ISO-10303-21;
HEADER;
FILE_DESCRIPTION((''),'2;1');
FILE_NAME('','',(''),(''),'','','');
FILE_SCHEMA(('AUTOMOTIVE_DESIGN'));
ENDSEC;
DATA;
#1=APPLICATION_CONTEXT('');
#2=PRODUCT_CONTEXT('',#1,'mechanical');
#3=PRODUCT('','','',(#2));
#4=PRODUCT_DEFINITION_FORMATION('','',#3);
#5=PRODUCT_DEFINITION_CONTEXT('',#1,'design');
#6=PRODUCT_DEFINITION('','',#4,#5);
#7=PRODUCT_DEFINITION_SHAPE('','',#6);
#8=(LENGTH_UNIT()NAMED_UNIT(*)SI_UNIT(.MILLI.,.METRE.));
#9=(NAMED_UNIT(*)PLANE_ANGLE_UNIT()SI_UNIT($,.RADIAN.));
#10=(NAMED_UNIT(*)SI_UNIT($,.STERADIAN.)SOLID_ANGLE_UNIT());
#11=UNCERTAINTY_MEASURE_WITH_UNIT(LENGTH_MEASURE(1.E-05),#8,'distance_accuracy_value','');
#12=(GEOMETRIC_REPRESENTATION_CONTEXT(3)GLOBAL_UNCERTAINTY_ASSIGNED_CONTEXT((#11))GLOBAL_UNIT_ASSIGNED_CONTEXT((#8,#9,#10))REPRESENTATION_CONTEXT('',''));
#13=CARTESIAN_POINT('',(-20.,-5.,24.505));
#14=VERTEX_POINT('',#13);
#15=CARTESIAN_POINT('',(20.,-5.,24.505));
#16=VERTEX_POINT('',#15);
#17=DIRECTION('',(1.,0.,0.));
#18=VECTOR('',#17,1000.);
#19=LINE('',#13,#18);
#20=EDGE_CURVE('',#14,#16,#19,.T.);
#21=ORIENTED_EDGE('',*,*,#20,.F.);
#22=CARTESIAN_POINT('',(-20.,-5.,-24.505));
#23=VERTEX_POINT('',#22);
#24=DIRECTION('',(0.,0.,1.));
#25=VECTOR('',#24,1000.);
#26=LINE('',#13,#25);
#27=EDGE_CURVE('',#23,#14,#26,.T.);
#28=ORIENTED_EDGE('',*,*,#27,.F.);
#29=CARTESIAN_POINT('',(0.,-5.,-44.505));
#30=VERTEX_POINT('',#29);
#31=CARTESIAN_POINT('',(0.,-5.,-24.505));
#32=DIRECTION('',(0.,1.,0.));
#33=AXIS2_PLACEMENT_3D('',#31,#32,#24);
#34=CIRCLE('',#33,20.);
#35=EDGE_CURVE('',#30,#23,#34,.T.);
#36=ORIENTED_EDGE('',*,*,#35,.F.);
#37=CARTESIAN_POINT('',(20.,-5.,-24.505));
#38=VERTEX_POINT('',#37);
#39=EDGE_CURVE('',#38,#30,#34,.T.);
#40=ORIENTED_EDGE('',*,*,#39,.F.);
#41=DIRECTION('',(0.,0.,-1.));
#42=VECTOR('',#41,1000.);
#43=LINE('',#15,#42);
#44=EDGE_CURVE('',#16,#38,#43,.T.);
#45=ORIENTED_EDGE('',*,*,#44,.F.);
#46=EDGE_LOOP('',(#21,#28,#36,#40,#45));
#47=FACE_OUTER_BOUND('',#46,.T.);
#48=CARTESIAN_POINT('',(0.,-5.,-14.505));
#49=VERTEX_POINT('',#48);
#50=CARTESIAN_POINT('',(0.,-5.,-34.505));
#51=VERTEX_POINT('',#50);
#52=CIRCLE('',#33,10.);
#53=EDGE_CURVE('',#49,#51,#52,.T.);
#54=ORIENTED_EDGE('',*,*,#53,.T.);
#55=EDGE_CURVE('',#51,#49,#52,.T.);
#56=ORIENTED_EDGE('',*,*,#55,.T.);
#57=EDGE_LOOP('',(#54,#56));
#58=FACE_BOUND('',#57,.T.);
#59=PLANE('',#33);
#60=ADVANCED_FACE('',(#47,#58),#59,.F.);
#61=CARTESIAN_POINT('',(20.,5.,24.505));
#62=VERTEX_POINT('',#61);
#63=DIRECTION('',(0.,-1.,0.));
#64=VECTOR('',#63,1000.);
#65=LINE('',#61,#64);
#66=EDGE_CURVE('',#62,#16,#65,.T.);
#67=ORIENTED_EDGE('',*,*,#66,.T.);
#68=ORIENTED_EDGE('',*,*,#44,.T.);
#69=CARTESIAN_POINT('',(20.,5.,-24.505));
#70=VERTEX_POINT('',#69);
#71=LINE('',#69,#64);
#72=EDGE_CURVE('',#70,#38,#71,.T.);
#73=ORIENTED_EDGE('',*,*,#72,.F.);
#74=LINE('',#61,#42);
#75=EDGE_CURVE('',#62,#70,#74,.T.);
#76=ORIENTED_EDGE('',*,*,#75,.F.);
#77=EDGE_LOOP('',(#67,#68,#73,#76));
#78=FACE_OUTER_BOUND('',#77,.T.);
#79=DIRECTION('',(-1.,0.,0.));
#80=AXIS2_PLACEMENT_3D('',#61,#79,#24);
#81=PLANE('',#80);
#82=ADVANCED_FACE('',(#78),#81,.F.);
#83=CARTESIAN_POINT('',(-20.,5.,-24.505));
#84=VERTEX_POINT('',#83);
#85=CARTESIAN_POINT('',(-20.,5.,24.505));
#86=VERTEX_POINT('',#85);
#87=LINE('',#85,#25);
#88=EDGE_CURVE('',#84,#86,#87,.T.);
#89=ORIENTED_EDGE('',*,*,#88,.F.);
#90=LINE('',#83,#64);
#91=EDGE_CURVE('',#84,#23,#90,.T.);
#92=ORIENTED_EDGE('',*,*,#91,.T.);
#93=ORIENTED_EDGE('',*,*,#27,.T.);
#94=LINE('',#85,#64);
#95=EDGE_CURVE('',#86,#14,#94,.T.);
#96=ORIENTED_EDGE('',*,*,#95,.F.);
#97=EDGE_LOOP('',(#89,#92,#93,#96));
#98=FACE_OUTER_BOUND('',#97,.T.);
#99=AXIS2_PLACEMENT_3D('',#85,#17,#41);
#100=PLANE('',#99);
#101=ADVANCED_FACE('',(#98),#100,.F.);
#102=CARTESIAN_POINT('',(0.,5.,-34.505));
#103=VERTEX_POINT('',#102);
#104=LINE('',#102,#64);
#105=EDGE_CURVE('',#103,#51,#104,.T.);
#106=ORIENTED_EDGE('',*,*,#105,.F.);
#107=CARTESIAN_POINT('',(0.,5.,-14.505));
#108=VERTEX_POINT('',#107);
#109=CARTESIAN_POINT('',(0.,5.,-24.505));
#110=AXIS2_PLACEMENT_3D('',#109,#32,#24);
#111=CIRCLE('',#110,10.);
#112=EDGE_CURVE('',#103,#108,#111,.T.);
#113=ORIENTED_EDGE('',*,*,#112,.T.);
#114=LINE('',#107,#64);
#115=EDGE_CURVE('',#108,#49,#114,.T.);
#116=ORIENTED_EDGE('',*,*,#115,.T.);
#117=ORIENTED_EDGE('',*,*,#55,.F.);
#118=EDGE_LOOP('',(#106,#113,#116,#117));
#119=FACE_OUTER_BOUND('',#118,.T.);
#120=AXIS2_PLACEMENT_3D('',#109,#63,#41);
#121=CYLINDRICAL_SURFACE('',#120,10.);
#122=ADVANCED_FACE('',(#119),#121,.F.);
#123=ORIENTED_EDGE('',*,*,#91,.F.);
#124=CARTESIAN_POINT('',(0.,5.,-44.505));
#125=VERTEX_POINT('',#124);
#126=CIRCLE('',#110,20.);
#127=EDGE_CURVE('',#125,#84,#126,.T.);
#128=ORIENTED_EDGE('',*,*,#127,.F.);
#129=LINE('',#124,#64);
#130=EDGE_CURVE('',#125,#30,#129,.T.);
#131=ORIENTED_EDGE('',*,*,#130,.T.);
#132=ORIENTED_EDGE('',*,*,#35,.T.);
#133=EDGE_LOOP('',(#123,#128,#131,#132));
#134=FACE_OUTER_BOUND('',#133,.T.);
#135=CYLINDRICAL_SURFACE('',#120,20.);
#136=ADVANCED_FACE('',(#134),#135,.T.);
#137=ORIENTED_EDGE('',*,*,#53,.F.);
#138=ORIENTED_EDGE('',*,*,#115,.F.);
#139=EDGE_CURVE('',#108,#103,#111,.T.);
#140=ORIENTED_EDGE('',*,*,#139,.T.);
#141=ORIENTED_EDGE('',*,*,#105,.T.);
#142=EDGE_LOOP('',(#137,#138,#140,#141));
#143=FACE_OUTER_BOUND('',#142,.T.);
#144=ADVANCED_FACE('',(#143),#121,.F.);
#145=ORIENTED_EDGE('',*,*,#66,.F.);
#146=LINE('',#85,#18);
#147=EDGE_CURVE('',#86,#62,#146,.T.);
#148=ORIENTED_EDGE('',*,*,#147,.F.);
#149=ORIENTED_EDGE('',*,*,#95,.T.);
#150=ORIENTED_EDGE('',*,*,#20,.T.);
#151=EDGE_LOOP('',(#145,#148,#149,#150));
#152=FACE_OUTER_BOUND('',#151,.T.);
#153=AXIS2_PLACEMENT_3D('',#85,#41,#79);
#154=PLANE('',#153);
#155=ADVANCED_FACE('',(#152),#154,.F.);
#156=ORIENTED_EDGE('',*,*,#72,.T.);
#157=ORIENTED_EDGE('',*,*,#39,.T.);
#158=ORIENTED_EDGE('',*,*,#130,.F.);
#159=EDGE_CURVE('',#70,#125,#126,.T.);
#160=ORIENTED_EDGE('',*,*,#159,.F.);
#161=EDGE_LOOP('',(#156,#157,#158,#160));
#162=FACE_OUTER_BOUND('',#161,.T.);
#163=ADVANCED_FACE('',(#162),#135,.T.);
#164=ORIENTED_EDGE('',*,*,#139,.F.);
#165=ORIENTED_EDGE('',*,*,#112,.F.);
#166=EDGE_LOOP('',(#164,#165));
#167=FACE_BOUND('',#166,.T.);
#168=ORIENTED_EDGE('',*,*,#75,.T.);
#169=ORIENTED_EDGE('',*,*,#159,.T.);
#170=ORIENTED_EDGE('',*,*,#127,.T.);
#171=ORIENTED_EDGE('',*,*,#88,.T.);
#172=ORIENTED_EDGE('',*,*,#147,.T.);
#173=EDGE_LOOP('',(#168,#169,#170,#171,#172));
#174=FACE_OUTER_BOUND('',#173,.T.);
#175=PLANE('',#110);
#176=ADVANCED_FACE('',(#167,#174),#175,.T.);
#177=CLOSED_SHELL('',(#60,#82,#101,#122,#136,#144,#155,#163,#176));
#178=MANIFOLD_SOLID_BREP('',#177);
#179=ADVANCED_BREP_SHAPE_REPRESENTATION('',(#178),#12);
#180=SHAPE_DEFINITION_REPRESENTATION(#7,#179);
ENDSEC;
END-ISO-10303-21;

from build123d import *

# Parameters (mm, degrees)
SKETCH_1_R      = 10
EXTRUDE_1_DEPTH = 5


with BuildPart() as part:
    # 草图1 → 凸台-拉伸1 (new, symmetric)
    with BuildSketch(Plane(origin=(0, 0, 0), x_dir=(1, 0, 0), z_dir=(0, 1, 0))):
        with BuildLine():
            Line((-20, -24.505), (20, -24.505))
            Line((20, -24.505), (20, 24.505))
            ThreePointArc((20, 24.505), (0, 44.505), (-20, 24.505))
            Line((-20, 24.505), (-20, -24.505))
        make_face()
        with Locations(Location((0, 24.505, 0), (0, 0, 270))):
            Circle(SKETCH_1_R, mode=Mode.SUBTRACT)
    extrude(amount=EXTRUDE_1_DEPTH, both=True)


solid = part.part
